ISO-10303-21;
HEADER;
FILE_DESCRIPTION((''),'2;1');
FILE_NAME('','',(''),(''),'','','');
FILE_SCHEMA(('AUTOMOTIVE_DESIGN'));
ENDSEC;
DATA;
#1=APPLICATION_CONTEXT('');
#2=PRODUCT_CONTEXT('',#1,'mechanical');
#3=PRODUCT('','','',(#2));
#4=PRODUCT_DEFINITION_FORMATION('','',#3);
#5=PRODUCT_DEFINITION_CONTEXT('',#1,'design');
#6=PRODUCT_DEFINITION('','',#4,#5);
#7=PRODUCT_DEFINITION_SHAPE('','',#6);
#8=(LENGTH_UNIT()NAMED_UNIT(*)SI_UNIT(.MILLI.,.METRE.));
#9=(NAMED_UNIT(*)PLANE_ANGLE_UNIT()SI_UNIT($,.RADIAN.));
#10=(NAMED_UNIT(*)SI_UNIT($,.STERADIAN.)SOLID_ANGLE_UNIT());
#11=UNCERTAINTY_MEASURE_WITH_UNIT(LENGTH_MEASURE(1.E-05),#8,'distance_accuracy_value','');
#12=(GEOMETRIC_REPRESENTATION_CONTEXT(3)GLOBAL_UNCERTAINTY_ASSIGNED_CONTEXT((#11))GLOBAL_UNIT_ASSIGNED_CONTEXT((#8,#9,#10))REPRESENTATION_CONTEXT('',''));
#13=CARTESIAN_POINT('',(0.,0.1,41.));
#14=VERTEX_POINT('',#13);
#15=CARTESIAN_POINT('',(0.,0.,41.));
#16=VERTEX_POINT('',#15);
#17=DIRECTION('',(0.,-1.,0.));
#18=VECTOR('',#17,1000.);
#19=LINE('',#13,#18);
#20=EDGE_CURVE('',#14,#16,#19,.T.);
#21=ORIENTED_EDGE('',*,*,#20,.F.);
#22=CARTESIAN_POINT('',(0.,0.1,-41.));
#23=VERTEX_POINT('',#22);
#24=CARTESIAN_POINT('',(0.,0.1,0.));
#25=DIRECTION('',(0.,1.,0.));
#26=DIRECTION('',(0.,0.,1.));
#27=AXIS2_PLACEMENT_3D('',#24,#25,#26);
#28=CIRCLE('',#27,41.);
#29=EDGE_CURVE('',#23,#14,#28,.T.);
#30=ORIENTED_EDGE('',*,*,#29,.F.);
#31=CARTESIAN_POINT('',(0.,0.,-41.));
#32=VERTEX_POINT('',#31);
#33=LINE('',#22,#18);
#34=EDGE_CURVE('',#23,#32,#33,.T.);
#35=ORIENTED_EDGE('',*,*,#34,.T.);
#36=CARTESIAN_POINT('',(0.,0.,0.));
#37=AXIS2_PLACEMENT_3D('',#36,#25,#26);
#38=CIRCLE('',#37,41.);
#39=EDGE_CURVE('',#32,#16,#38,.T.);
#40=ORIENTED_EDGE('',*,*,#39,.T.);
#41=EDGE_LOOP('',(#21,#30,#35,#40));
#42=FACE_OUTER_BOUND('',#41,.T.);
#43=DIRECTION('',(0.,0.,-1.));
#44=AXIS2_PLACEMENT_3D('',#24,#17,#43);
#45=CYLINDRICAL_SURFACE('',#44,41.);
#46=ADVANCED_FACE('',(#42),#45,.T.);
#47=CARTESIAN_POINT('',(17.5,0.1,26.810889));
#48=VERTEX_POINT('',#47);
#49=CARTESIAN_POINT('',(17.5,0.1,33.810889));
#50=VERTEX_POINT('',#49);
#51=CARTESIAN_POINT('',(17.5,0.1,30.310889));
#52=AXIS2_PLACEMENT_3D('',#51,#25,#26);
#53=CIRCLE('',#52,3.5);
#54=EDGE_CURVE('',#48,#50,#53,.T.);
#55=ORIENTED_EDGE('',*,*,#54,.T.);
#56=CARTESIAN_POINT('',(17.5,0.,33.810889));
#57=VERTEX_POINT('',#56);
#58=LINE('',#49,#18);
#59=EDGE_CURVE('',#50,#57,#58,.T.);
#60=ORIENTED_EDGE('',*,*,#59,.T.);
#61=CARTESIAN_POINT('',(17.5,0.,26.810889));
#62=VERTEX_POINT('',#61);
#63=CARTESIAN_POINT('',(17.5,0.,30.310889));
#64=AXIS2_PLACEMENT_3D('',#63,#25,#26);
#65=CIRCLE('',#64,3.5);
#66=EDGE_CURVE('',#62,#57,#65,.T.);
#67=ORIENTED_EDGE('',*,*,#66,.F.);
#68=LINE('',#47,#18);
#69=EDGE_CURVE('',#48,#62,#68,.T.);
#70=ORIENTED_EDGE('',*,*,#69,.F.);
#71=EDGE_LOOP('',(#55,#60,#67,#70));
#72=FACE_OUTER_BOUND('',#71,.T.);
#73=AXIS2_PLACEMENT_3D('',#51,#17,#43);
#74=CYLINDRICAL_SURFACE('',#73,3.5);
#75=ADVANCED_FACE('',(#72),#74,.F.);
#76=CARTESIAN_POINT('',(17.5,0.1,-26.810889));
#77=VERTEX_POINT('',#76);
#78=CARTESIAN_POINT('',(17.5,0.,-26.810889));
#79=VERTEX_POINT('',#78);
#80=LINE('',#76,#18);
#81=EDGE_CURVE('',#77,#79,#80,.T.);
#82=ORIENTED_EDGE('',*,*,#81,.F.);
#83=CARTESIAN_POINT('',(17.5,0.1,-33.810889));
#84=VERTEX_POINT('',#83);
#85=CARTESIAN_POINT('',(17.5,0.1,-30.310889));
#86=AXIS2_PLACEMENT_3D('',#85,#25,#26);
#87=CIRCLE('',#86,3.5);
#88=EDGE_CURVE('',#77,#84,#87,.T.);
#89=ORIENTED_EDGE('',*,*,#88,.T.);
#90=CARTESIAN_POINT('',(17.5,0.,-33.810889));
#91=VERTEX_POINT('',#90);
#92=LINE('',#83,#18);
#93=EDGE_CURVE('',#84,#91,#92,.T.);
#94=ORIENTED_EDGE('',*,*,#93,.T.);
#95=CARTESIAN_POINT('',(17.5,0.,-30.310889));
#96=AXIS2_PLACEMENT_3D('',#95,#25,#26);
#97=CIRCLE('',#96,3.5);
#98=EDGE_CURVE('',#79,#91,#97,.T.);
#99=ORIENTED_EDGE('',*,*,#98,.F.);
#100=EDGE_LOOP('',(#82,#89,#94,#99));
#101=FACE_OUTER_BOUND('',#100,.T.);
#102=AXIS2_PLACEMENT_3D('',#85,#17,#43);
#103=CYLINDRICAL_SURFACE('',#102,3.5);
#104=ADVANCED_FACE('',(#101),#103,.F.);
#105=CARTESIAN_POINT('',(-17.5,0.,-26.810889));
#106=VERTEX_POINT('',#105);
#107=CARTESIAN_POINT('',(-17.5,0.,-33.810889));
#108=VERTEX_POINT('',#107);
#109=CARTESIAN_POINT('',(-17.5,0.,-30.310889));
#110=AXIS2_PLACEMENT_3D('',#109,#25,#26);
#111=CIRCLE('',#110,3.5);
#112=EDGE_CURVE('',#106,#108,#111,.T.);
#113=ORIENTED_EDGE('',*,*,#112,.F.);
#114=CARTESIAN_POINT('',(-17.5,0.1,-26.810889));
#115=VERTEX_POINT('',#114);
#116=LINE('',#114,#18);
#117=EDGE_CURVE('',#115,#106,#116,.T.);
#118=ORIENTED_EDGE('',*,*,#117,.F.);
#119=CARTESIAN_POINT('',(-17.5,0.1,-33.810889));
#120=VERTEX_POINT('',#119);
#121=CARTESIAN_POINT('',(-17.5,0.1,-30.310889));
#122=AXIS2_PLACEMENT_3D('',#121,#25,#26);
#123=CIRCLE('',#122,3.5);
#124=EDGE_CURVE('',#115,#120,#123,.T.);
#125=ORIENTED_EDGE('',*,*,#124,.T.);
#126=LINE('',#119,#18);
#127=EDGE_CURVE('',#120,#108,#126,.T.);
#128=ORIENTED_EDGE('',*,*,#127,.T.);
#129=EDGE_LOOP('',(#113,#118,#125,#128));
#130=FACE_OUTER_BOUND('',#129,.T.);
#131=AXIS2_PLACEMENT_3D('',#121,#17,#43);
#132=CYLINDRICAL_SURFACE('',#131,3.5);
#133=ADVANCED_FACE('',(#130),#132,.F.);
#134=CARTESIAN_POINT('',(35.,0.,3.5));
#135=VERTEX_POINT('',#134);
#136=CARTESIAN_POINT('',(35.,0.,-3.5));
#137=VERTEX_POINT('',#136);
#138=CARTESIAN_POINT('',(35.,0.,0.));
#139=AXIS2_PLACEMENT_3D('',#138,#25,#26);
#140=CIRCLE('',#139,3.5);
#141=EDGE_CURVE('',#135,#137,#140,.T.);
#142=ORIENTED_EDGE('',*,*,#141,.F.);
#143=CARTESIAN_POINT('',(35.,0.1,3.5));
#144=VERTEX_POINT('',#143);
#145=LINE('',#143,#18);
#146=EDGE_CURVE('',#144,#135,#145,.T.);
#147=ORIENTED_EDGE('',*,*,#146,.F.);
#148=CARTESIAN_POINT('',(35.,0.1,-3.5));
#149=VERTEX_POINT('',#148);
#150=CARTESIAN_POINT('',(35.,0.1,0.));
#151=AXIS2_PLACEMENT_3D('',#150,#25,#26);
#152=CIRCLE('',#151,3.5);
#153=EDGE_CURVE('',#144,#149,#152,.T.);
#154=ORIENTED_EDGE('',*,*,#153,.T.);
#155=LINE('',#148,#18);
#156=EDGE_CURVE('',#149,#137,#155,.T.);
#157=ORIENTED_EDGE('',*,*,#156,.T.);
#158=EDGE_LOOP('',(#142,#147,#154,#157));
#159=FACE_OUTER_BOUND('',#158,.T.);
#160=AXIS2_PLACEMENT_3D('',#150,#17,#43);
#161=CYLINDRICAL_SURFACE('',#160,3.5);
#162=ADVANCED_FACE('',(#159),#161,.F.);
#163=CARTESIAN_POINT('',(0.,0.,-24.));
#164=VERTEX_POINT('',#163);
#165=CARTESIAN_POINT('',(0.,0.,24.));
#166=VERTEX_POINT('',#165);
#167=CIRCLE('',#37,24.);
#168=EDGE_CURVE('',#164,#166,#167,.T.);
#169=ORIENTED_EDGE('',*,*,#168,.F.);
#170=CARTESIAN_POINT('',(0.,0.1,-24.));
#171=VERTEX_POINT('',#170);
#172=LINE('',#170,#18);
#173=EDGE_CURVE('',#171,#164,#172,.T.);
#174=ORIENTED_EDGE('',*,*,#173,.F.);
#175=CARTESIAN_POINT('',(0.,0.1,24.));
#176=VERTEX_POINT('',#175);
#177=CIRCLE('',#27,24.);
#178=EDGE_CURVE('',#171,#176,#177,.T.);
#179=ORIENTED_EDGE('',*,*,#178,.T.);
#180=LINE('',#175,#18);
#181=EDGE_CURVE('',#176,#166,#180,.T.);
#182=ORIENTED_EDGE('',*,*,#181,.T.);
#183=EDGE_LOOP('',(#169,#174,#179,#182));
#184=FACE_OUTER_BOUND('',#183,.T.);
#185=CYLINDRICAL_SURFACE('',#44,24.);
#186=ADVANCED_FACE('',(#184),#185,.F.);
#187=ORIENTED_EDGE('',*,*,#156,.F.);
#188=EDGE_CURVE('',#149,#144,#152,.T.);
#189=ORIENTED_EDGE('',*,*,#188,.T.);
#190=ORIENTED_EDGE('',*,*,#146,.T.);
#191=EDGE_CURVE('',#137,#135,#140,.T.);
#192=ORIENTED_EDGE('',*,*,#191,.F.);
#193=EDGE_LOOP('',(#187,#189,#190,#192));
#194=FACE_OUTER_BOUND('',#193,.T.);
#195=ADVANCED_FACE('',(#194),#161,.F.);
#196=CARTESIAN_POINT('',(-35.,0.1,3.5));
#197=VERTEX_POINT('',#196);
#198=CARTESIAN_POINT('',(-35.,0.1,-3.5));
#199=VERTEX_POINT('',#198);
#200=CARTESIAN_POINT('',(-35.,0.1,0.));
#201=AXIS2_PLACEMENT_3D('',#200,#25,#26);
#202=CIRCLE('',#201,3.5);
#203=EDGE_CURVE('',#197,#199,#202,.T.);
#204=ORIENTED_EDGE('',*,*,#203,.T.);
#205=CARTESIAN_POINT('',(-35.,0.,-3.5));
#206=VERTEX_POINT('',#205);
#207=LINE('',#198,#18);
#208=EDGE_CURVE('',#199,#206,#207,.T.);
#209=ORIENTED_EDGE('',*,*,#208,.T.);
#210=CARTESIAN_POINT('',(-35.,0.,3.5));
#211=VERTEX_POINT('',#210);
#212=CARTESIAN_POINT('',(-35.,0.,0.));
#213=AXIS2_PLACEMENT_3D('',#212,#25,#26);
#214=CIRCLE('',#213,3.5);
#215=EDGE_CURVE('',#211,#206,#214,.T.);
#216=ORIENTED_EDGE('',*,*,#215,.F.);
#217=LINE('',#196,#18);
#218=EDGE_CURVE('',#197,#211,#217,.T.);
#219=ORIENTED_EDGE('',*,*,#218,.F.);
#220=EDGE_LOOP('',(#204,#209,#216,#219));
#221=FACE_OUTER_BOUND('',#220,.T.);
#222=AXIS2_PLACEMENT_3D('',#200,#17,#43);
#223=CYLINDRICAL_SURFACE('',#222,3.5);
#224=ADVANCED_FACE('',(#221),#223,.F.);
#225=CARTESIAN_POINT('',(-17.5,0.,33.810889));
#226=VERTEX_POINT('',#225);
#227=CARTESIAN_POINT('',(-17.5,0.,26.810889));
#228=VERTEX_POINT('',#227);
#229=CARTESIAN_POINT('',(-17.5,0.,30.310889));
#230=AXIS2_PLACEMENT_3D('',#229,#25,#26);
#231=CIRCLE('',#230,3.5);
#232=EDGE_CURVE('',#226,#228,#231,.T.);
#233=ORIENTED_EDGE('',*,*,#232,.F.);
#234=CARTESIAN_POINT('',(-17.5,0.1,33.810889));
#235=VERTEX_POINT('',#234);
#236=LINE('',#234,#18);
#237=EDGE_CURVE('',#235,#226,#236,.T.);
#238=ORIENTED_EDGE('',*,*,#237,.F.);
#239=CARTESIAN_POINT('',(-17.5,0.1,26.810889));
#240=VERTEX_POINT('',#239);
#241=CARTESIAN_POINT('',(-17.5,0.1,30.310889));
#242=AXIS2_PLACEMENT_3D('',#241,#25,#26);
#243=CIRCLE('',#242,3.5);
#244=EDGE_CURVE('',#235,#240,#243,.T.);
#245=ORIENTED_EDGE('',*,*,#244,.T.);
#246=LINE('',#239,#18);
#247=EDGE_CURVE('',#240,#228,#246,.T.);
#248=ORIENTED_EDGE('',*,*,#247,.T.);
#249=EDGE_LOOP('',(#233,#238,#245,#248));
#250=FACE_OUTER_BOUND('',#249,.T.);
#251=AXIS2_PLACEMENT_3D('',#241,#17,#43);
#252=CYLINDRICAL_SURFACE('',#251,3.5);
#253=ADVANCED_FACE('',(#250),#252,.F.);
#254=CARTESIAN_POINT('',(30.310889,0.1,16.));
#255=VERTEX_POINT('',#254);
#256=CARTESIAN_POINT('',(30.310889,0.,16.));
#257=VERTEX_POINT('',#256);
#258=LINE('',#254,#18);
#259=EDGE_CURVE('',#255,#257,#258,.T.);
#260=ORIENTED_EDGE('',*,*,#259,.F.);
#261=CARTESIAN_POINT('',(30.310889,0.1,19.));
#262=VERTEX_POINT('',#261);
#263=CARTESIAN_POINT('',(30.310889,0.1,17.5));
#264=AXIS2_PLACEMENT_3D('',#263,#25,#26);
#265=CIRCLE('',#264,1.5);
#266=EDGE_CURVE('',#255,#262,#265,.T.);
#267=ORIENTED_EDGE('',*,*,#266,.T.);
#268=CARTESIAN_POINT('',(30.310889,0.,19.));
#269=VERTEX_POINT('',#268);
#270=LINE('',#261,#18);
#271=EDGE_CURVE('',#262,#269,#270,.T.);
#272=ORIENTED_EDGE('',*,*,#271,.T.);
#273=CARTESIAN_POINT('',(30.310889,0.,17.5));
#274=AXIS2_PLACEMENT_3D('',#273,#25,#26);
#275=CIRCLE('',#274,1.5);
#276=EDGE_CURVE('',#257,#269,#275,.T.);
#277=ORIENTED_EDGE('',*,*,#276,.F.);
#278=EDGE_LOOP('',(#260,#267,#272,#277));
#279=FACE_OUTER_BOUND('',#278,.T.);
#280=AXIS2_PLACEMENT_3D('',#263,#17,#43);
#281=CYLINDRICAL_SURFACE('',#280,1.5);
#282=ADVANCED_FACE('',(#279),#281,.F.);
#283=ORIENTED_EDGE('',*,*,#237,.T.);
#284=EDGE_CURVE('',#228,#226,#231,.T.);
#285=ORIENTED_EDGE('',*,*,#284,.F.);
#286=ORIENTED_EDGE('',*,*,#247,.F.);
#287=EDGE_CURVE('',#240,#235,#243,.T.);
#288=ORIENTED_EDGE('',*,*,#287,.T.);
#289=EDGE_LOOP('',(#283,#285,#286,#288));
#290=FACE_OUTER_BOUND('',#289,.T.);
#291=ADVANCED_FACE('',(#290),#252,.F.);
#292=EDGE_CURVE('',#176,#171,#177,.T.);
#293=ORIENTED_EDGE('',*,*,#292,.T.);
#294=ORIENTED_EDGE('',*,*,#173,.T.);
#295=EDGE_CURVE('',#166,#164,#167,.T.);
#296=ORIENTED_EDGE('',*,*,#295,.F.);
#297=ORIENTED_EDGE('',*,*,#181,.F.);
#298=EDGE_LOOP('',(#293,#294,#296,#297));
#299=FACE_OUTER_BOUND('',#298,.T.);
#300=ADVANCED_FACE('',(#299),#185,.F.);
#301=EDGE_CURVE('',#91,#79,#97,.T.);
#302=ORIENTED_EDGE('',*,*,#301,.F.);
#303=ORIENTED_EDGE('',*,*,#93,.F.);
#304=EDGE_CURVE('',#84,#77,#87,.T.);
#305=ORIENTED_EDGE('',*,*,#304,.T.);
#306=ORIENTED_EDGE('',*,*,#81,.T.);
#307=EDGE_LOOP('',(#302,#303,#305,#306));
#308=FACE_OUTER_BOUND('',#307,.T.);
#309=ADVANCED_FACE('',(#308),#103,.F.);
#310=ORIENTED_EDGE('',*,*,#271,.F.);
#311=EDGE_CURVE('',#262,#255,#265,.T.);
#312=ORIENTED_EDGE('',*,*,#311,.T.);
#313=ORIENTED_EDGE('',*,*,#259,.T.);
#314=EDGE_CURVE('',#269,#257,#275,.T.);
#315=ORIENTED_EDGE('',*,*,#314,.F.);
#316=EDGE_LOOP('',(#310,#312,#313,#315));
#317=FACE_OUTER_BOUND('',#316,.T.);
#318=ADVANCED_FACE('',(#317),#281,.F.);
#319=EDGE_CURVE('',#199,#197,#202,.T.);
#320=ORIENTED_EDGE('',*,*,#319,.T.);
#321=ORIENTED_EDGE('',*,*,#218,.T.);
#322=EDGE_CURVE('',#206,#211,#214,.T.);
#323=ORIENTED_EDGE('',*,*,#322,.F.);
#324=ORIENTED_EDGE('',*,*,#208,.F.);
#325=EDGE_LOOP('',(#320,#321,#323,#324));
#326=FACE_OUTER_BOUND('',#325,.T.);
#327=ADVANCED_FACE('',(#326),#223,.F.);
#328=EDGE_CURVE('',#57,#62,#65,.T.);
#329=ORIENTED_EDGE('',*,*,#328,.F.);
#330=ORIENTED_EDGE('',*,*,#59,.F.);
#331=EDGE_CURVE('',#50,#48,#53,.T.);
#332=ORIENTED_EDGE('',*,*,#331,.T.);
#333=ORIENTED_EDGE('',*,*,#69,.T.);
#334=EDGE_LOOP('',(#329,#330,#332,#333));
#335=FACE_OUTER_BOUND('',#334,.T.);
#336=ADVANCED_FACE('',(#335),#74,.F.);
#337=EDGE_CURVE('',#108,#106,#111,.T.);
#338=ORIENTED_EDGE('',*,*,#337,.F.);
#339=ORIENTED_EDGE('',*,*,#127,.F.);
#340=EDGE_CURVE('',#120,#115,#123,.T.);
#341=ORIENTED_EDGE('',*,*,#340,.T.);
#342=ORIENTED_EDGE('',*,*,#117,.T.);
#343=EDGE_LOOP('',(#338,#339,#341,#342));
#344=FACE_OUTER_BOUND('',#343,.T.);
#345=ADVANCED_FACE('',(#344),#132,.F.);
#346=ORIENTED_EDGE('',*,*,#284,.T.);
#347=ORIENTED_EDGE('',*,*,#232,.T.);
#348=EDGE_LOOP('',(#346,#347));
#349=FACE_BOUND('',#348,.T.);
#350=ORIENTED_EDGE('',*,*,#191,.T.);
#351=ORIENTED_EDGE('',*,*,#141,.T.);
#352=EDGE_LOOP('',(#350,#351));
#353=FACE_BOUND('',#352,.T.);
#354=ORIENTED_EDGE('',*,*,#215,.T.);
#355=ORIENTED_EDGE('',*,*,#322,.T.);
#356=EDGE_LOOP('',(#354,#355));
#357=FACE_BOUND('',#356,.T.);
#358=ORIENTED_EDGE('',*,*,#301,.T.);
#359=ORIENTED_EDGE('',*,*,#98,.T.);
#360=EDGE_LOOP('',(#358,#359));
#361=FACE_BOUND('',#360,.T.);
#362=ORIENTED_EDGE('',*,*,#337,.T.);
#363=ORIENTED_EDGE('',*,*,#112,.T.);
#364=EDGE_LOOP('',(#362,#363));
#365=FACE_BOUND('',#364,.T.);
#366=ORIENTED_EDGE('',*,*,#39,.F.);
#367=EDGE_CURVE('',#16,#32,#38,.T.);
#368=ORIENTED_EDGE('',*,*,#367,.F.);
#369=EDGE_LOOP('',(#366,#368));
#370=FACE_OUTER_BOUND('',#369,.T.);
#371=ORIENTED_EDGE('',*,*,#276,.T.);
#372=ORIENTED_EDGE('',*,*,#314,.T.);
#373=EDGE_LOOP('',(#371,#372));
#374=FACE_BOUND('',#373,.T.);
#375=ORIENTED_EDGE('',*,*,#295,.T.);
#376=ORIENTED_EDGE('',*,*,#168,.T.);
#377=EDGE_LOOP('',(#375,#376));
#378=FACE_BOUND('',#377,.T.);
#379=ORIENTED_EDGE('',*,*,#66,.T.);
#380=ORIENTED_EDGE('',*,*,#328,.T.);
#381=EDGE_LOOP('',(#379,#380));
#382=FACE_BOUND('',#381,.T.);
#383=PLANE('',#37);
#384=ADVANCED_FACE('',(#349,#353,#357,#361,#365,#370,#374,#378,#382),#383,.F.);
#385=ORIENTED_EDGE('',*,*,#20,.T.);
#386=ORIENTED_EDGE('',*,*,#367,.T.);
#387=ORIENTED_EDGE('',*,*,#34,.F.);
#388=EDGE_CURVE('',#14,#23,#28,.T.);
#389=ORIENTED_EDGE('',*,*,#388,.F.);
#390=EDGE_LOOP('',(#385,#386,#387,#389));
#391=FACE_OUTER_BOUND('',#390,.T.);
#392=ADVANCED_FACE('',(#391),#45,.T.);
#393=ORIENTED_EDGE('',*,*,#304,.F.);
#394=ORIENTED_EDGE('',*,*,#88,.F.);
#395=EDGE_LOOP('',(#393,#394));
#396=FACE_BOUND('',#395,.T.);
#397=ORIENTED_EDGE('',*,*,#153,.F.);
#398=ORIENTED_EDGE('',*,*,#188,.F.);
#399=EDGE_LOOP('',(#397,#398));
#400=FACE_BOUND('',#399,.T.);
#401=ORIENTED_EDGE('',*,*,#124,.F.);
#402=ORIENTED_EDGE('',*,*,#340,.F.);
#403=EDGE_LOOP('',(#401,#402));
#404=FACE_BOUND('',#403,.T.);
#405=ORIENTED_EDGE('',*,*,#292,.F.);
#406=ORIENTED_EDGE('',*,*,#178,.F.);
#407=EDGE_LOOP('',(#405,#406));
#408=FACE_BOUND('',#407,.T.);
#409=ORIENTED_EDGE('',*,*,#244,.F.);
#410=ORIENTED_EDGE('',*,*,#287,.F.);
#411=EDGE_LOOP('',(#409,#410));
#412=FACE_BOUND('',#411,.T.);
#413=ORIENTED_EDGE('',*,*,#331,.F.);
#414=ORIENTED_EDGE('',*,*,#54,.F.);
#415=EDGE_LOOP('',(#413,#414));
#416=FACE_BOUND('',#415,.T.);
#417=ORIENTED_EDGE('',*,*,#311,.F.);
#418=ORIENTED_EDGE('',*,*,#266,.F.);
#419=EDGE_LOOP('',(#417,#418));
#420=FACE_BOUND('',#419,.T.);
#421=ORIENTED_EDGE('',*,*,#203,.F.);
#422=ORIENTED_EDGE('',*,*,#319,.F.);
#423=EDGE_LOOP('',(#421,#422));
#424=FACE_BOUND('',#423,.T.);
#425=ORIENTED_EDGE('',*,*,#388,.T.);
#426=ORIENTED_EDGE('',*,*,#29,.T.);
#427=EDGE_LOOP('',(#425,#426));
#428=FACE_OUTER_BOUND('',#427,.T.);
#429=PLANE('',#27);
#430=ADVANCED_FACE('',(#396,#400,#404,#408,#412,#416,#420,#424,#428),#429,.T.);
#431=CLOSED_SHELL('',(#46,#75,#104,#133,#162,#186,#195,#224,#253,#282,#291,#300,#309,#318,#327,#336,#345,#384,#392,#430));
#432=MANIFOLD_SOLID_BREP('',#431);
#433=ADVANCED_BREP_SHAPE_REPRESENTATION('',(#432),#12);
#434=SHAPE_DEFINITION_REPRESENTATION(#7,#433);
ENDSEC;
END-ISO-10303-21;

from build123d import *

# Parameters (mm, degrees)
SKETCH1_R           = 41
SKETCH1_R_2         = 24
SKETCH1_R_3         = 3.5
SKETCH1_R_4         = 1.5
BOSS_EXTRUDE1_DEPTH = 0.1


with BuildPart() as part:
    # Sketch1 → Boss-Extrude1 (new body)
    with BuildSketch(Plane(origin=(0, 0, 0), x_dir=(1, 0, 0), z_dir=(0, 1, 0))):
        with Locations(Location((0, 0, 0), (0, 0, 270))):
            Circle(SKETCH1_R)
        with Locations(Location((0, 0, 0), (0, 0, 270))):
            Circle(SKETCH1_R_2, mode=Mode.SUBTRACT)
        with Locations(Location((35, 0, 0), (0, 0, 270))):
            Circle(SKETCH1_R_3, mode=Mode.SUBTRACT)
        with Locations(Location((17.5, -30.310889132, 0), (0, 0, 270))):
            Circle(SKETCH1_R_3, mode=Mode.SUBTRACT)
        with Locations(Location((-17.5, -30.310889132, 0), (0, 0, 270))):
            Circle(SKETCH1_R_3, mode=Mode.SUBTRACT)
        with Locations(Location((-35, 0, 0), (0, 0, 270))):
            Circle(SKETCH1_R_3, mode=Mode.SUBTRACT)
        with Locations(Location((-17.5, 30.310889132, 0), (0, 0, 270))):
            Circle(SKETCH1_R_3, mode=Mode.SUBTRACT)
        with Locations(Location((17.5, 30.310889132, 0), (0, 0, 270))):
            Circle(SKETCH1_R_3, mode=Mode.SUBTRACT)
        with Locations(Location((30.310889132, -17.5, 0), (0, 0, 270))):
            Circle(SKETCH1_R_4, mode=Mode.SUBTRACT)
    extrude(amount=BOSS_EXTRUDE1_DEPTH)


solid = part.part
